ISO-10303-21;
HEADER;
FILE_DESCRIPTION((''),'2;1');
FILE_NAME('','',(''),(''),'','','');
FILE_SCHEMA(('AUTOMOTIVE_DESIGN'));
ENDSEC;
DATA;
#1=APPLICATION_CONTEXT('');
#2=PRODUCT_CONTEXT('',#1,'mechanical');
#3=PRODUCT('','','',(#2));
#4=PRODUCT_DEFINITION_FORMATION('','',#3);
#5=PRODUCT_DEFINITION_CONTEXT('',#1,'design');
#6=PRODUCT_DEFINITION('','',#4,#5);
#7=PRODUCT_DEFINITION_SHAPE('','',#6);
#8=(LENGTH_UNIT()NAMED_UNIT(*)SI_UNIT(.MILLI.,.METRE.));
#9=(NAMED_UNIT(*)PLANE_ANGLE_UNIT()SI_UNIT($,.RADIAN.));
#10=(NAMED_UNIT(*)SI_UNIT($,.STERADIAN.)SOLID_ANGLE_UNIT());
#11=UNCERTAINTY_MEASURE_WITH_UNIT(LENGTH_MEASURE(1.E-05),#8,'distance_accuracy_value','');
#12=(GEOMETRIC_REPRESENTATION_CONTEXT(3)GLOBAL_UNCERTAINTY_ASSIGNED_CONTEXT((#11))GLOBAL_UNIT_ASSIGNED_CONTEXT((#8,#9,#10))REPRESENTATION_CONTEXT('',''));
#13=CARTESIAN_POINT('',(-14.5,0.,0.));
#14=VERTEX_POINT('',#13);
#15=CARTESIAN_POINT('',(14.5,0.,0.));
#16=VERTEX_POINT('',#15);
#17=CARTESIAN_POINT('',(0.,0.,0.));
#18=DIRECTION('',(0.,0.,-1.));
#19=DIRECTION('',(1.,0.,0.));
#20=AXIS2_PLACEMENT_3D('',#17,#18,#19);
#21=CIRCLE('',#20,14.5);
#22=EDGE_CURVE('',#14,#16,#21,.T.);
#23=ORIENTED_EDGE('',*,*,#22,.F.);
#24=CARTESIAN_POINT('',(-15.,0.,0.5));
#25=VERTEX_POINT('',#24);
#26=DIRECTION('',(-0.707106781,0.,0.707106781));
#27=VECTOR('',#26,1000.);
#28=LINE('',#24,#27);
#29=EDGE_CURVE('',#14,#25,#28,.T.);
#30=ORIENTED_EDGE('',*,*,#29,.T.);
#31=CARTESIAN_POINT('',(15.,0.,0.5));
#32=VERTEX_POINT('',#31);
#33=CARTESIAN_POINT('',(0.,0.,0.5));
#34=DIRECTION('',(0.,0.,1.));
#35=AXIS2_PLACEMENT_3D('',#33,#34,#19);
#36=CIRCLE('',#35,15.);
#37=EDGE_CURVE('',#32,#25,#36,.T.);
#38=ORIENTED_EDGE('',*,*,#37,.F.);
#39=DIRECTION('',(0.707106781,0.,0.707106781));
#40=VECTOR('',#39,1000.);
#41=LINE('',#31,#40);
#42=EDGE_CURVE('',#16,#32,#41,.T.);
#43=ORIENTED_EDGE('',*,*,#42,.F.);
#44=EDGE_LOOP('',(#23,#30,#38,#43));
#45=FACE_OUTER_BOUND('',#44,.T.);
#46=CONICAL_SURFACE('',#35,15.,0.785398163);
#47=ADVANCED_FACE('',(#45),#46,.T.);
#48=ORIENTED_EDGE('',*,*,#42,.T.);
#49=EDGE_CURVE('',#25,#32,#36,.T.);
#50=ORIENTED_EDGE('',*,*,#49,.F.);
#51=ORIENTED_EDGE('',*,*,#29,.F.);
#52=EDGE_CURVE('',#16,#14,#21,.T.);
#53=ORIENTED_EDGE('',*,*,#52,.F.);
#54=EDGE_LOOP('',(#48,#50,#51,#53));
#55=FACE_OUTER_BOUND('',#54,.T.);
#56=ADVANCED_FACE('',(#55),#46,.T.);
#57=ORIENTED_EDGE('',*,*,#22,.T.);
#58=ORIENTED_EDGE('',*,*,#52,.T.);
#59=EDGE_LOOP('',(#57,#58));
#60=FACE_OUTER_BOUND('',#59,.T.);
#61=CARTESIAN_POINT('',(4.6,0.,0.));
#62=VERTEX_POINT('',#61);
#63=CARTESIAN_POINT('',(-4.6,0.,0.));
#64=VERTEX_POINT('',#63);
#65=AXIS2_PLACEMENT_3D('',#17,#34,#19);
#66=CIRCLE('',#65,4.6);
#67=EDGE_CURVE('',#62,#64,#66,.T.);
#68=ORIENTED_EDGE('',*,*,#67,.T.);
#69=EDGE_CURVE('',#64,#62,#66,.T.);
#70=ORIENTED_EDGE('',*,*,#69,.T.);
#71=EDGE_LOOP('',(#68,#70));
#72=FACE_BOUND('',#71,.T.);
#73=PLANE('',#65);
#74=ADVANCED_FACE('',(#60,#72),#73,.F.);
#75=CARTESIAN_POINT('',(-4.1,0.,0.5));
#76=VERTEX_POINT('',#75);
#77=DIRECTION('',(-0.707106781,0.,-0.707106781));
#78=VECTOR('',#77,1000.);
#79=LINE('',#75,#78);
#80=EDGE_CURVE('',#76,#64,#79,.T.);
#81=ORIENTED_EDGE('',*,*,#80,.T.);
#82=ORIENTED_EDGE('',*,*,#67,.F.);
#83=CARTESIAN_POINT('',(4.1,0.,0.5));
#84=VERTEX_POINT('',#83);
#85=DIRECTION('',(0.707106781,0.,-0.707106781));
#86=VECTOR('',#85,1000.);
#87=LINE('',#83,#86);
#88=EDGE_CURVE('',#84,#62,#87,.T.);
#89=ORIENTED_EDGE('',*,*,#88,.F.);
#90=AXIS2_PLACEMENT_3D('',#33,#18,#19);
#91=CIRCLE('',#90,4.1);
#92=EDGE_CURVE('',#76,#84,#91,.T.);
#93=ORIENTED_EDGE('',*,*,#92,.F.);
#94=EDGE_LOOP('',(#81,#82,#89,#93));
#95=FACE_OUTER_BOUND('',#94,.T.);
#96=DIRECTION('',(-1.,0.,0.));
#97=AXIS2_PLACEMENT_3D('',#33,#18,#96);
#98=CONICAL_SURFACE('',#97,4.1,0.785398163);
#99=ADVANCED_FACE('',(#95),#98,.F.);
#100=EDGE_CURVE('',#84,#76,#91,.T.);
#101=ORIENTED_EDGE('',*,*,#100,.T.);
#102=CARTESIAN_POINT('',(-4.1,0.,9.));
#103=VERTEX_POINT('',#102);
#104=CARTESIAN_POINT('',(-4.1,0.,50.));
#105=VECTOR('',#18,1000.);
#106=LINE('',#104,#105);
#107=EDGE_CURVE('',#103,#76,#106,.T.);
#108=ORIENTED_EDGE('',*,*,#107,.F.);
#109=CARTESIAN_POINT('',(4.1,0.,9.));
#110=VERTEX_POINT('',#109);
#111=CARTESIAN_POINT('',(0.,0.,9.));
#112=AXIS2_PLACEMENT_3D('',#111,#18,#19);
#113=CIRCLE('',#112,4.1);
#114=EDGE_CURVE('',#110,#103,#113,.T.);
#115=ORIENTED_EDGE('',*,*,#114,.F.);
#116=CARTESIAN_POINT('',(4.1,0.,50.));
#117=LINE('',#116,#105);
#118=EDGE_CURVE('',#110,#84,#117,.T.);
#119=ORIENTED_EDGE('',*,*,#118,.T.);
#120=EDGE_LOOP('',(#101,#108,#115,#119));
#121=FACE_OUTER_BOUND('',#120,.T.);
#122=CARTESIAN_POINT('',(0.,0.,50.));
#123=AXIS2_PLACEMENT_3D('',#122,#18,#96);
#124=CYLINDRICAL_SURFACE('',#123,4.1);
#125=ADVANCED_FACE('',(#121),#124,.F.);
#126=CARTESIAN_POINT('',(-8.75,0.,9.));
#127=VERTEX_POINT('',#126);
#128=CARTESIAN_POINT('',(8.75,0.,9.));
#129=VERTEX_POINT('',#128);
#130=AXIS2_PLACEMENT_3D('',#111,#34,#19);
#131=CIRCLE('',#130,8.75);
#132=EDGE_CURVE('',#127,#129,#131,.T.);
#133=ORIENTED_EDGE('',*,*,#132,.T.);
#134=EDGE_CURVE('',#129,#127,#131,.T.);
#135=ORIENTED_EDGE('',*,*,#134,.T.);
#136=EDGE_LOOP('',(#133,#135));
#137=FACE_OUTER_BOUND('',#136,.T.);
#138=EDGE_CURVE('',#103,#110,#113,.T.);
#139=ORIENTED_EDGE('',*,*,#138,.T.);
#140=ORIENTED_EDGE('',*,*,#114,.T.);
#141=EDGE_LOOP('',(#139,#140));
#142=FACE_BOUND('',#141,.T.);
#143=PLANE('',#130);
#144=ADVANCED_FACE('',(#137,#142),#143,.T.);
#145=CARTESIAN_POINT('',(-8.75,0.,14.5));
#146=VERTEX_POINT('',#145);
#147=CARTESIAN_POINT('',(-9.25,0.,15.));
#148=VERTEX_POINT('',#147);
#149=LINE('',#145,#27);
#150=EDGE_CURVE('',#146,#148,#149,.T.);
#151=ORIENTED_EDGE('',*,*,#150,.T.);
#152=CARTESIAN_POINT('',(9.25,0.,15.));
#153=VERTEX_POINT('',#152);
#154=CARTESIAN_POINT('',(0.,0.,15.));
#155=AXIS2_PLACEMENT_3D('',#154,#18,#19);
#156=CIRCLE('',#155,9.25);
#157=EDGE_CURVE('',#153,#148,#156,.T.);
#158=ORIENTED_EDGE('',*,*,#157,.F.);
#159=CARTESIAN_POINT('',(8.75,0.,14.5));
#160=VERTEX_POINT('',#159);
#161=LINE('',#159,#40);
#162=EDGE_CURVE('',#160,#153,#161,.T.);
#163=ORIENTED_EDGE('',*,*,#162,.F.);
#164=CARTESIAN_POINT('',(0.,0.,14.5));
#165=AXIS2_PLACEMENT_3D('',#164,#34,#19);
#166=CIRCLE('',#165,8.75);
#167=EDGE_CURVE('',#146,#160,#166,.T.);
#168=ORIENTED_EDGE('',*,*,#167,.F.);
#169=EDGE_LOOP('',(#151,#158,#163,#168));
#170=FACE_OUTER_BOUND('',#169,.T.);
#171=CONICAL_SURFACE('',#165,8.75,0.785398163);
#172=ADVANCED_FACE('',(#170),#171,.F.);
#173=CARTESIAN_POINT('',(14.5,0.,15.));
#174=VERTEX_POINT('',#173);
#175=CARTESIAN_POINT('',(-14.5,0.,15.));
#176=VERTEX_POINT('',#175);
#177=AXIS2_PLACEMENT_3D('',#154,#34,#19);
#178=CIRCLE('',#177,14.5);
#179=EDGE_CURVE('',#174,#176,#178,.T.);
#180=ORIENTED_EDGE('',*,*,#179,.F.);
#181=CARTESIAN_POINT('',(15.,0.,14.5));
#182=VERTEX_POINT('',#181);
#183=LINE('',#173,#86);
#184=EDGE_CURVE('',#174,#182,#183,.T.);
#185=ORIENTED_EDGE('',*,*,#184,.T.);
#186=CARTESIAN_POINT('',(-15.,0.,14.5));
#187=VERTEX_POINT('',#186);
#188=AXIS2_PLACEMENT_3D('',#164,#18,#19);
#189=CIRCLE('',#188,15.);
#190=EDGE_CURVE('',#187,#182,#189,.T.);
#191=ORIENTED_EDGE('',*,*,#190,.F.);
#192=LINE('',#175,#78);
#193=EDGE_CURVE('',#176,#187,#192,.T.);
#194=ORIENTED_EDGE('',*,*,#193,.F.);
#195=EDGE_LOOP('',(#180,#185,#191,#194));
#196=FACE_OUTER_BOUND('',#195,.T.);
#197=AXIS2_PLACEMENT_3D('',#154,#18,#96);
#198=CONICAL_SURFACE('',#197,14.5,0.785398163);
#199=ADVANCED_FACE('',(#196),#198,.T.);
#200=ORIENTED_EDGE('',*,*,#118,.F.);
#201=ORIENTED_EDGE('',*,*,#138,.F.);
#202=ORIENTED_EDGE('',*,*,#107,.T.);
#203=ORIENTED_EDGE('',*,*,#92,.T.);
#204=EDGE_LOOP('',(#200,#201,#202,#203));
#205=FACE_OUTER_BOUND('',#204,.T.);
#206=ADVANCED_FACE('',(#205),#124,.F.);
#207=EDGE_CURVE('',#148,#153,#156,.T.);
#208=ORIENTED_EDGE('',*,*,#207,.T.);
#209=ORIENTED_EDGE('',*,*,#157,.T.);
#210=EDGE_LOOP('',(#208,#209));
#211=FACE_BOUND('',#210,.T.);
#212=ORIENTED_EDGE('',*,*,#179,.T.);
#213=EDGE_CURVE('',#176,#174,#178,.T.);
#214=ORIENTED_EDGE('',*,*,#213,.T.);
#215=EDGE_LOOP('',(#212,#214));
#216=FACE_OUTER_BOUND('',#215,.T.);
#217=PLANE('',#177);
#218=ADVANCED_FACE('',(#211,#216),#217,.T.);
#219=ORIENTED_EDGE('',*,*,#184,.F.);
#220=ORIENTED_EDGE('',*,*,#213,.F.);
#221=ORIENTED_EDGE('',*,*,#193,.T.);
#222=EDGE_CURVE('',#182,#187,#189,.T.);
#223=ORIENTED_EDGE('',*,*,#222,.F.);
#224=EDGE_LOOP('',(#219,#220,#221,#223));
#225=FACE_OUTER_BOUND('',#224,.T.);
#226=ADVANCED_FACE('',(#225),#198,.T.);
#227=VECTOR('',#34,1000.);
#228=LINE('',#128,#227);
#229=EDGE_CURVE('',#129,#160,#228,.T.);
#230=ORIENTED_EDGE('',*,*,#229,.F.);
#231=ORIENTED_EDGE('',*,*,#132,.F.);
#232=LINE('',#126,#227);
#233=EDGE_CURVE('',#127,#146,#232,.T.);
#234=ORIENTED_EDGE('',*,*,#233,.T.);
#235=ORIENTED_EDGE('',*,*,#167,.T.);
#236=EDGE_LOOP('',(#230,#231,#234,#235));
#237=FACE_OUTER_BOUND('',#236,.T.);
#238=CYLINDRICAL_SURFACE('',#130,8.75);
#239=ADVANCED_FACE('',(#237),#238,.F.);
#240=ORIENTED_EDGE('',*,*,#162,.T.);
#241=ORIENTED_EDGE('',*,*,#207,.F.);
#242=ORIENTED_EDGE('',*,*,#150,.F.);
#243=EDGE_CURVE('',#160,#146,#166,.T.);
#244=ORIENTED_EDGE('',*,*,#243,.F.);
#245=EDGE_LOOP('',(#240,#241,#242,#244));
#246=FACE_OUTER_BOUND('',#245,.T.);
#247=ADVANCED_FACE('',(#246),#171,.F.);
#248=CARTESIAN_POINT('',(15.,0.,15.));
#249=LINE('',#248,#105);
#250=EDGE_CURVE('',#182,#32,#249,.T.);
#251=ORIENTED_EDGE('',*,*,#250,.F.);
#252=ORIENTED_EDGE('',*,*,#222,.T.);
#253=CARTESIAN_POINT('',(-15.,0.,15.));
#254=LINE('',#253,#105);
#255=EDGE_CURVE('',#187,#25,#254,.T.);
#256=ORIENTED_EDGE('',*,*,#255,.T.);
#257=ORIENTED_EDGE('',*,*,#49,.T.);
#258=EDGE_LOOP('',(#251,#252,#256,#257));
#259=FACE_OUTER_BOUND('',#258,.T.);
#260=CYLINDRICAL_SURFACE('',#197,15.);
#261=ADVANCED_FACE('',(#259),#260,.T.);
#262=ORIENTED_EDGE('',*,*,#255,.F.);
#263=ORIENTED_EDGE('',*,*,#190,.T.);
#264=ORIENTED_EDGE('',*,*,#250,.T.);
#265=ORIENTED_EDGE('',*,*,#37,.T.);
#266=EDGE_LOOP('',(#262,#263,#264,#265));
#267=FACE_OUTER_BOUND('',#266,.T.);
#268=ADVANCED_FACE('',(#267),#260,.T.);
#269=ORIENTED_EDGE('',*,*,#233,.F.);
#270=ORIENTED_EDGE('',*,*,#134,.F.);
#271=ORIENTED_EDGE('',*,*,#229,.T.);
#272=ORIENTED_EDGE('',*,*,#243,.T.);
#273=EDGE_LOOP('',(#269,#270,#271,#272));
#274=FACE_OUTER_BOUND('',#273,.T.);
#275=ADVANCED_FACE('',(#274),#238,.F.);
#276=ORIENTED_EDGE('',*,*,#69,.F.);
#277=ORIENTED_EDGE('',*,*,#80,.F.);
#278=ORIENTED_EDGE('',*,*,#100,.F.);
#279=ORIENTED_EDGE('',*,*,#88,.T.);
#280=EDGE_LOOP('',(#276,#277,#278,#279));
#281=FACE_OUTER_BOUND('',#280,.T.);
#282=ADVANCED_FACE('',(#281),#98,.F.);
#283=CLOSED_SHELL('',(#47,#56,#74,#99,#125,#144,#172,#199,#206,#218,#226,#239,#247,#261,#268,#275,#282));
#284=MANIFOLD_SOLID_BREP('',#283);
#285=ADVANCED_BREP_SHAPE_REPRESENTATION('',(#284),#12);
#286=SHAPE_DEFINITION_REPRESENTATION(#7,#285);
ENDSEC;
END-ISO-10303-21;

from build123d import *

# Parameters (mm, degrees)
SKETCH1_R           = 15
BOSS_EXTRUDE1_DEPTH = 15
SKETCH6_R           = 4.1
CUT_EXTRUDE3_DEPTH  = 50
SKETCH8_R           = 8.75
CUT_EXTRUDE5_DEPTH  = 6
CHAMFER2_SIZE       = 0.5
CHAMFER3_SIZE       = 0.5


with BuildPart() as part:
    # Sketch1 → Boss-Extrude1 (new body)
    with BuildSketch(Plane.XY):
        Circle(SKETCH1_R)
    extrude(amount=BOSS_EXTRUDE1_DEPTH)

    # Sketch6 → Cut-Extrude3 (cut)
    with BuildSketch(Plane(origin=(0, 0, 0), x_dir=(-1, 0, 0), z_dir=(0, 0, -1))):
        Circle(SKETCH6_R)
    extrude(amount=-CUT_EXTRUDE3_DEPTH, mode=Mode.SUBTRACT)

    # Sketch8 → Cut-Extrude5 (cut)
    with BuildSketch(Plane.XY.offset(15)):
        Circle(SKETCH8_R)
    extrude(amount=-CUT_EXTRUDE5_DEPTH, mode=Mode.SUBTRACT)

    # Chamfer2
    chamfer2_edges = [part.edges().sort_by_distance(p)[0] for p in [
        (-8.75, 0, 15),
    ]]
    chamfer(chamfer2_edges, length=CHAMFER2_SIZE)

    # Chamfer3
    chamfer3_edges = [part.edges().sort_by_distance(p)[0] for p in [
        (-15, 0, 0),
        (-15, 0, 15),
        (4.1, 0, 0),
    ]]
    chamfer(chamfer3_edges, length=CHAMFER3_SIZE)


solid = part.part
